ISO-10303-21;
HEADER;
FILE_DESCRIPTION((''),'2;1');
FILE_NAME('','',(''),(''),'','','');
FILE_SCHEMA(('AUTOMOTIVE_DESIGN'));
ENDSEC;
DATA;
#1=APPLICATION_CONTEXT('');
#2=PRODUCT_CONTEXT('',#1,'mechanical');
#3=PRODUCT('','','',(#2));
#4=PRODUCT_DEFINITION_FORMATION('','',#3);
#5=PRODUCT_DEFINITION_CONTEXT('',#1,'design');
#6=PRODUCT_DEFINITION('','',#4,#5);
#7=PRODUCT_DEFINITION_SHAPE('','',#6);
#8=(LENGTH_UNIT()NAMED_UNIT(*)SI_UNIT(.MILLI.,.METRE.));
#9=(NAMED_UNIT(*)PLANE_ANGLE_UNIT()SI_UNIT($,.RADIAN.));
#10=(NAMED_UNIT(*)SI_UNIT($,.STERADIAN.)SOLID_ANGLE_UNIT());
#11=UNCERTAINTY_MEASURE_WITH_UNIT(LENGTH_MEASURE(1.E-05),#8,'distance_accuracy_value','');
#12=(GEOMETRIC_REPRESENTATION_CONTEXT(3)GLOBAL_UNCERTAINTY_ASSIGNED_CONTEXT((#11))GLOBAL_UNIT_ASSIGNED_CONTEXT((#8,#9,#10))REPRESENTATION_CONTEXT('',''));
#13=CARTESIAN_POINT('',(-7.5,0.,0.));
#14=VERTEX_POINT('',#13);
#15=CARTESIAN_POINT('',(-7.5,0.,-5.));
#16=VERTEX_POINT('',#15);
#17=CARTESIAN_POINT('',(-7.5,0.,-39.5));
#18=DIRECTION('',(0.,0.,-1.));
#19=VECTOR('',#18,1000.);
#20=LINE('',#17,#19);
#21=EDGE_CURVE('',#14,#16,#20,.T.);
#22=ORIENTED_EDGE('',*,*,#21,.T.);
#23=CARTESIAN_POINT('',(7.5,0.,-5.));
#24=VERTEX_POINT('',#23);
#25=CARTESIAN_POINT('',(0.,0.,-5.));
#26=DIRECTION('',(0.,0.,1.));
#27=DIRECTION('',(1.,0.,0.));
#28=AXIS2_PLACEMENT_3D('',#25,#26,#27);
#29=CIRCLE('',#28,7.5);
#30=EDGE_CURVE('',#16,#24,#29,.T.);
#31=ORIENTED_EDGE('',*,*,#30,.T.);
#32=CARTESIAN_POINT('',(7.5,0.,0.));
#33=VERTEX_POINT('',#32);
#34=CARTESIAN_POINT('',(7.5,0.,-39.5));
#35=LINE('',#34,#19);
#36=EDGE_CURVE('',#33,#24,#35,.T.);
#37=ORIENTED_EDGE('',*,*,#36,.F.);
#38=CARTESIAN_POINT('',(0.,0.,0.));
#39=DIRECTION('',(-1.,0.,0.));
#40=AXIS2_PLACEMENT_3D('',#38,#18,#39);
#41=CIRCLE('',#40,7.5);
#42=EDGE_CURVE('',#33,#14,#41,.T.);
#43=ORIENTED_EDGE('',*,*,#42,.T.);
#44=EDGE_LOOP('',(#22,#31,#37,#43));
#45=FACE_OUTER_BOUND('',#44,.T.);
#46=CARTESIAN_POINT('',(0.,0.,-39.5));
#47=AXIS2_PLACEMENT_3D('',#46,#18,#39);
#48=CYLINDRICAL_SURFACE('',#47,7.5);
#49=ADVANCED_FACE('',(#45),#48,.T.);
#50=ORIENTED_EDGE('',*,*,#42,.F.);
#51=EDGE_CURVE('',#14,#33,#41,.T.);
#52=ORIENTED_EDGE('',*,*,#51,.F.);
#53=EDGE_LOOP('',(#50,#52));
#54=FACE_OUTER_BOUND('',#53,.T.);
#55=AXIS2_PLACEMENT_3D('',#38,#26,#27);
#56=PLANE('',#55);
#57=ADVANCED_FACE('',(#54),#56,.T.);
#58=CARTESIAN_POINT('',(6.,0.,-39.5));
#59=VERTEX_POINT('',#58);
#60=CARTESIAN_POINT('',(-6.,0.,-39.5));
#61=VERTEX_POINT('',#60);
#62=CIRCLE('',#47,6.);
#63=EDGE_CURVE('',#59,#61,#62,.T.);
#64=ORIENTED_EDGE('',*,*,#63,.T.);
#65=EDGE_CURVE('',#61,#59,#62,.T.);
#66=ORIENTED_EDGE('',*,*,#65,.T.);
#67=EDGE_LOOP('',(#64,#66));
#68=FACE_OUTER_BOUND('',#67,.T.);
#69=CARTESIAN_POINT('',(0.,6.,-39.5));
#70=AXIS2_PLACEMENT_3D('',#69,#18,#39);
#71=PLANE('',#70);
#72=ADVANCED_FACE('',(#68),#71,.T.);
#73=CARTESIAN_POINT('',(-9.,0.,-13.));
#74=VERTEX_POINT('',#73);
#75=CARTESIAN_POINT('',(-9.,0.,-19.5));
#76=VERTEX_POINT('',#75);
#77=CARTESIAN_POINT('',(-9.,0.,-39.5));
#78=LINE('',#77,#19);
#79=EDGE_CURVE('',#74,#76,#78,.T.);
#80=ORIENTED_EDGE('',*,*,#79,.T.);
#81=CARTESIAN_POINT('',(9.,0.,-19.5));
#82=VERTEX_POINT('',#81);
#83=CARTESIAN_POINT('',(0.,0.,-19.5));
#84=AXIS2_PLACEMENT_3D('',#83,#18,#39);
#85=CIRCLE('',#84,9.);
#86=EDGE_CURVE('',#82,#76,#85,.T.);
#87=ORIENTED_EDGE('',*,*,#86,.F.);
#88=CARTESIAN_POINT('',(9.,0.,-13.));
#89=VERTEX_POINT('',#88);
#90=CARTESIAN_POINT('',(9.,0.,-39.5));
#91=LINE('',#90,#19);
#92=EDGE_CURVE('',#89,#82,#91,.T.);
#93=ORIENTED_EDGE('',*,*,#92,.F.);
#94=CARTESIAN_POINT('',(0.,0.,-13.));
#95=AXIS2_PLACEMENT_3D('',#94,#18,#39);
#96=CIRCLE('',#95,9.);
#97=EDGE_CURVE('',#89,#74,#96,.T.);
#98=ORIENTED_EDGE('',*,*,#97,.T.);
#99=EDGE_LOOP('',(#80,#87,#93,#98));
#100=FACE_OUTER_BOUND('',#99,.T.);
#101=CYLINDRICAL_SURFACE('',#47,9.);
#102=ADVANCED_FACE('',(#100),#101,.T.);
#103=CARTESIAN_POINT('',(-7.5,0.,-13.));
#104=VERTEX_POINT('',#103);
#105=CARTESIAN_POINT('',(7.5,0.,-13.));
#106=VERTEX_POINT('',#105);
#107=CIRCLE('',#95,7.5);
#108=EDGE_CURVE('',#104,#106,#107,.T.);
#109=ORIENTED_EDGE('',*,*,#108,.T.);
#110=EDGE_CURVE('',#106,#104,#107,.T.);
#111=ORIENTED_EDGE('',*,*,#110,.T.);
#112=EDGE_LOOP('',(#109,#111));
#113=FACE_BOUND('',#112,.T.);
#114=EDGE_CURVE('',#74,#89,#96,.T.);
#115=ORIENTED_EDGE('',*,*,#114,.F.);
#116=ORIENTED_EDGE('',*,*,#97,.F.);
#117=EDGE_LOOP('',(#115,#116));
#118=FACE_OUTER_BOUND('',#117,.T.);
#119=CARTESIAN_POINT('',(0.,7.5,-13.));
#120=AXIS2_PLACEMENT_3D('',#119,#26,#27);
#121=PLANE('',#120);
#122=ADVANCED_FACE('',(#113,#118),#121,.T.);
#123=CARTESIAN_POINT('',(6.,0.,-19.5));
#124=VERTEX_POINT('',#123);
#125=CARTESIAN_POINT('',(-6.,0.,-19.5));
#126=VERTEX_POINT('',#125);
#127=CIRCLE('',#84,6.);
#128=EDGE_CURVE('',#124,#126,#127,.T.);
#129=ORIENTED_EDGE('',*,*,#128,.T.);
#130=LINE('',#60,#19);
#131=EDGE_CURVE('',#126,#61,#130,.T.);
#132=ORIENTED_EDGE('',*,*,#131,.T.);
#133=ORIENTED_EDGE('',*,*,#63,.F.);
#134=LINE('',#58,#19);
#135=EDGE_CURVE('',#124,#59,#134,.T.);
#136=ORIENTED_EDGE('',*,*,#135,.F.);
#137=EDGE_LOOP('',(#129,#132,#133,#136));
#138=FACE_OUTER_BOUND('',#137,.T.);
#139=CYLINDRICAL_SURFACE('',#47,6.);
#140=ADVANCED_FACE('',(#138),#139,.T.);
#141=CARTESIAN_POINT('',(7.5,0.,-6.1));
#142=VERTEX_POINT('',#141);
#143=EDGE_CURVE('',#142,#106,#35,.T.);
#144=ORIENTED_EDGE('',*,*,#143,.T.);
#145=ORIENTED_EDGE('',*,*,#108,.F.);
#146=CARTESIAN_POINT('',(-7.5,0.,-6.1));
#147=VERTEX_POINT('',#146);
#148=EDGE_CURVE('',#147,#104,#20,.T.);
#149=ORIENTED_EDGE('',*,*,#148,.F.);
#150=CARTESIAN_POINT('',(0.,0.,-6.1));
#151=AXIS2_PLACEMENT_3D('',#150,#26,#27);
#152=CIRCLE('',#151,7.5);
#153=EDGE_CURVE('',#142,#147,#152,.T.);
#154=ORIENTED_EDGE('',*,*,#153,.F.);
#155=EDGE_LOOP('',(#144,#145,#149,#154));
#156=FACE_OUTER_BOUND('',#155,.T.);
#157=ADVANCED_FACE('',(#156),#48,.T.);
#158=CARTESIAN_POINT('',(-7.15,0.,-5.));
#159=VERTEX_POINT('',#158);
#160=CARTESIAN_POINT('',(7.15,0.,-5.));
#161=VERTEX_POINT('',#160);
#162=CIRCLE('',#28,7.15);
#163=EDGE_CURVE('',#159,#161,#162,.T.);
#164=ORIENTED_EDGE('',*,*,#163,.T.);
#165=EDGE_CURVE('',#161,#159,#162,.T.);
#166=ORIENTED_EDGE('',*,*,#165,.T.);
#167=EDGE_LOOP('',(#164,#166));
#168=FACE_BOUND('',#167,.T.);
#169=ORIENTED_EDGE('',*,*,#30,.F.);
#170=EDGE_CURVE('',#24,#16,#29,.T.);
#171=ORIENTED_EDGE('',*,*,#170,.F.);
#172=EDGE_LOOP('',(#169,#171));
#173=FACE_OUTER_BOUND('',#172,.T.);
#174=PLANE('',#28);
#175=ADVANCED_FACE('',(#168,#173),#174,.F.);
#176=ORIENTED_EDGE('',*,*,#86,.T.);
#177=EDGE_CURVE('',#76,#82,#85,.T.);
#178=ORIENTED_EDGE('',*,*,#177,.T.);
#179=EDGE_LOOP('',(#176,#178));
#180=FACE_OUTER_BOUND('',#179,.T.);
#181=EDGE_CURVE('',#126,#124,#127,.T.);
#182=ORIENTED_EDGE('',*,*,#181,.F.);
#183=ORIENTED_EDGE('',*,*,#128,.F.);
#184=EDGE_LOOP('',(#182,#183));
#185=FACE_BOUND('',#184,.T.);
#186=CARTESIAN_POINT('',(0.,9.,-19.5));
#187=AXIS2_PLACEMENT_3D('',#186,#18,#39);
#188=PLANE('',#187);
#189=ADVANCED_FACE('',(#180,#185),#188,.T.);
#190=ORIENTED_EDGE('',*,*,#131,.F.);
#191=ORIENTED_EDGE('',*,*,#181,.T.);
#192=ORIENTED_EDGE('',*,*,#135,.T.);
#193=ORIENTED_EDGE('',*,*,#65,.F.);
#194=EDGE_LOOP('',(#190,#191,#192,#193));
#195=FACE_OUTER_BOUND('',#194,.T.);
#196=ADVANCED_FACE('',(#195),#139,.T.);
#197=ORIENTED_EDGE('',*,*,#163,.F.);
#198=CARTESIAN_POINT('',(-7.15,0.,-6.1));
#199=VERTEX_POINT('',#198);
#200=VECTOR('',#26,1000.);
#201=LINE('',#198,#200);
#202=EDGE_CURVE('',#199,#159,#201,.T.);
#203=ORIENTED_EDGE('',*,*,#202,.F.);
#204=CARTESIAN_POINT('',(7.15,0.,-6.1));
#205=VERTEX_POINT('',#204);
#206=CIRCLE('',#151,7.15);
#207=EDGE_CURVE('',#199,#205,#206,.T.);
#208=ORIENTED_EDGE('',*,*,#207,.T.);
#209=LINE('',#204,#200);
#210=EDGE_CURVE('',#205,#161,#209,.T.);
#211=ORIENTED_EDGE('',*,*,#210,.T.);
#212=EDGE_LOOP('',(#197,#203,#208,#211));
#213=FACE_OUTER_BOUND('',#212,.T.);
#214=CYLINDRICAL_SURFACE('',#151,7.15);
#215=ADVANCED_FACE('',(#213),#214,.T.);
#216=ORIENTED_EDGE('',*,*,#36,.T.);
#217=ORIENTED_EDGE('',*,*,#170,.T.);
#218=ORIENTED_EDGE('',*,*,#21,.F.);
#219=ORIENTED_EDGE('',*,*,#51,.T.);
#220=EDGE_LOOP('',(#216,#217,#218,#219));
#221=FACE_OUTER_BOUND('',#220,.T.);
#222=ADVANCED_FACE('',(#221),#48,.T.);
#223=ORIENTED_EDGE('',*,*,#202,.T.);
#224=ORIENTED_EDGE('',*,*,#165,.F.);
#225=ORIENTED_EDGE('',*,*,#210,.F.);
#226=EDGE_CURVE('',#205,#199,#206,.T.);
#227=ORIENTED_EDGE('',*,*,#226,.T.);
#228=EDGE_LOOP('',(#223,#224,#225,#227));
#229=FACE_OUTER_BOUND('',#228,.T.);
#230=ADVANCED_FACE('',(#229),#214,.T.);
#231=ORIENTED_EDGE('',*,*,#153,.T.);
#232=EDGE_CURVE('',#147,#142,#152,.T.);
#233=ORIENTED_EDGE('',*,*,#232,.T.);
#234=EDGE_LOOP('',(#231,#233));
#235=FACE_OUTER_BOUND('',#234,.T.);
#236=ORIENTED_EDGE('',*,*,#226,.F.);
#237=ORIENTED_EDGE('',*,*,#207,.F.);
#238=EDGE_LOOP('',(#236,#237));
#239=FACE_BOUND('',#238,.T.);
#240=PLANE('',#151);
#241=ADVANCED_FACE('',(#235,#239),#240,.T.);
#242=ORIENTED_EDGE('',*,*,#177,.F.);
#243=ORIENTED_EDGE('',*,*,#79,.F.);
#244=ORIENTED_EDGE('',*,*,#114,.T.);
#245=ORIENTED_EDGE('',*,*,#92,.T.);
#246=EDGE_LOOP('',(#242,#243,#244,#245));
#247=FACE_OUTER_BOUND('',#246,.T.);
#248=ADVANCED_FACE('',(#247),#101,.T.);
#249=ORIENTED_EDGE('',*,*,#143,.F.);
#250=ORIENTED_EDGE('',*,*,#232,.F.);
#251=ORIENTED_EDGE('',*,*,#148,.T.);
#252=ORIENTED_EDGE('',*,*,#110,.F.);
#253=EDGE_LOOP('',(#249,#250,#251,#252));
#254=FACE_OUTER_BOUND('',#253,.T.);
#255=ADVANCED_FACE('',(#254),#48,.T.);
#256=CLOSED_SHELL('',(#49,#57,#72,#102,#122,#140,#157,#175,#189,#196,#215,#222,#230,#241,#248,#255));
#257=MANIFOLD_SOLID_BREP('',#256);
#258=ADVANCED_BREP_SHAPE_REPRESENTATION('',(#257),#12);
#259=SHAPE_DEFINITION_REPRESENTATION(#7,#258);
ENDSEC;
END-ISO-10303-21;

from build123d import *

# Parameters (mm, degrees)
CUT_EXTRUDE_START   = -1.1
SKETCH_3_R          = 7.5
SKETCH_3_R_2        = 7.15
CUT_EXTRUDE_1_DEPTH = 1.1


with BuildPart() as part:
    # 草图2 → 旋转1 (revolve)
    with BuildSketch(Plane(origin=(0, 0, 0), x_dir=(0, 0, -1), z_dir=(1, 0, 0)), mode=Mode.PRIVATE) as revolve_1_sk:
        Polygon((0, 0), (0, 7.5), (13, 7.5), (13, 9), (19.5, 9), (19.5, 6), (39.5, 6), (39.5, 0), align=None)
    revolve(revolve_1_sk.sketch.rotate(Axis((0, 0, -39.5), (0, 0, 1)), 90), axis=Axis((0, 0, -39.5), (0, 0, 1)))

    # 草图3 → 切除-拉伸1 (cut)
    with BuildSketch(Plane.XY.offset(-5).offset(CUT_EXTRUDE_START)):
        with Locations(Location((0, 0, 0), (0, 0, 180))):
            Circle(SKETCH_3_R)
        Circle(SKETCH_3_R_2, mode=Mode.SUBTRACT)
    extrude(amount=CUT_EXTRUDE_1_DEPTH, mode=Mode.SUBTRACT)


solid = part.part
